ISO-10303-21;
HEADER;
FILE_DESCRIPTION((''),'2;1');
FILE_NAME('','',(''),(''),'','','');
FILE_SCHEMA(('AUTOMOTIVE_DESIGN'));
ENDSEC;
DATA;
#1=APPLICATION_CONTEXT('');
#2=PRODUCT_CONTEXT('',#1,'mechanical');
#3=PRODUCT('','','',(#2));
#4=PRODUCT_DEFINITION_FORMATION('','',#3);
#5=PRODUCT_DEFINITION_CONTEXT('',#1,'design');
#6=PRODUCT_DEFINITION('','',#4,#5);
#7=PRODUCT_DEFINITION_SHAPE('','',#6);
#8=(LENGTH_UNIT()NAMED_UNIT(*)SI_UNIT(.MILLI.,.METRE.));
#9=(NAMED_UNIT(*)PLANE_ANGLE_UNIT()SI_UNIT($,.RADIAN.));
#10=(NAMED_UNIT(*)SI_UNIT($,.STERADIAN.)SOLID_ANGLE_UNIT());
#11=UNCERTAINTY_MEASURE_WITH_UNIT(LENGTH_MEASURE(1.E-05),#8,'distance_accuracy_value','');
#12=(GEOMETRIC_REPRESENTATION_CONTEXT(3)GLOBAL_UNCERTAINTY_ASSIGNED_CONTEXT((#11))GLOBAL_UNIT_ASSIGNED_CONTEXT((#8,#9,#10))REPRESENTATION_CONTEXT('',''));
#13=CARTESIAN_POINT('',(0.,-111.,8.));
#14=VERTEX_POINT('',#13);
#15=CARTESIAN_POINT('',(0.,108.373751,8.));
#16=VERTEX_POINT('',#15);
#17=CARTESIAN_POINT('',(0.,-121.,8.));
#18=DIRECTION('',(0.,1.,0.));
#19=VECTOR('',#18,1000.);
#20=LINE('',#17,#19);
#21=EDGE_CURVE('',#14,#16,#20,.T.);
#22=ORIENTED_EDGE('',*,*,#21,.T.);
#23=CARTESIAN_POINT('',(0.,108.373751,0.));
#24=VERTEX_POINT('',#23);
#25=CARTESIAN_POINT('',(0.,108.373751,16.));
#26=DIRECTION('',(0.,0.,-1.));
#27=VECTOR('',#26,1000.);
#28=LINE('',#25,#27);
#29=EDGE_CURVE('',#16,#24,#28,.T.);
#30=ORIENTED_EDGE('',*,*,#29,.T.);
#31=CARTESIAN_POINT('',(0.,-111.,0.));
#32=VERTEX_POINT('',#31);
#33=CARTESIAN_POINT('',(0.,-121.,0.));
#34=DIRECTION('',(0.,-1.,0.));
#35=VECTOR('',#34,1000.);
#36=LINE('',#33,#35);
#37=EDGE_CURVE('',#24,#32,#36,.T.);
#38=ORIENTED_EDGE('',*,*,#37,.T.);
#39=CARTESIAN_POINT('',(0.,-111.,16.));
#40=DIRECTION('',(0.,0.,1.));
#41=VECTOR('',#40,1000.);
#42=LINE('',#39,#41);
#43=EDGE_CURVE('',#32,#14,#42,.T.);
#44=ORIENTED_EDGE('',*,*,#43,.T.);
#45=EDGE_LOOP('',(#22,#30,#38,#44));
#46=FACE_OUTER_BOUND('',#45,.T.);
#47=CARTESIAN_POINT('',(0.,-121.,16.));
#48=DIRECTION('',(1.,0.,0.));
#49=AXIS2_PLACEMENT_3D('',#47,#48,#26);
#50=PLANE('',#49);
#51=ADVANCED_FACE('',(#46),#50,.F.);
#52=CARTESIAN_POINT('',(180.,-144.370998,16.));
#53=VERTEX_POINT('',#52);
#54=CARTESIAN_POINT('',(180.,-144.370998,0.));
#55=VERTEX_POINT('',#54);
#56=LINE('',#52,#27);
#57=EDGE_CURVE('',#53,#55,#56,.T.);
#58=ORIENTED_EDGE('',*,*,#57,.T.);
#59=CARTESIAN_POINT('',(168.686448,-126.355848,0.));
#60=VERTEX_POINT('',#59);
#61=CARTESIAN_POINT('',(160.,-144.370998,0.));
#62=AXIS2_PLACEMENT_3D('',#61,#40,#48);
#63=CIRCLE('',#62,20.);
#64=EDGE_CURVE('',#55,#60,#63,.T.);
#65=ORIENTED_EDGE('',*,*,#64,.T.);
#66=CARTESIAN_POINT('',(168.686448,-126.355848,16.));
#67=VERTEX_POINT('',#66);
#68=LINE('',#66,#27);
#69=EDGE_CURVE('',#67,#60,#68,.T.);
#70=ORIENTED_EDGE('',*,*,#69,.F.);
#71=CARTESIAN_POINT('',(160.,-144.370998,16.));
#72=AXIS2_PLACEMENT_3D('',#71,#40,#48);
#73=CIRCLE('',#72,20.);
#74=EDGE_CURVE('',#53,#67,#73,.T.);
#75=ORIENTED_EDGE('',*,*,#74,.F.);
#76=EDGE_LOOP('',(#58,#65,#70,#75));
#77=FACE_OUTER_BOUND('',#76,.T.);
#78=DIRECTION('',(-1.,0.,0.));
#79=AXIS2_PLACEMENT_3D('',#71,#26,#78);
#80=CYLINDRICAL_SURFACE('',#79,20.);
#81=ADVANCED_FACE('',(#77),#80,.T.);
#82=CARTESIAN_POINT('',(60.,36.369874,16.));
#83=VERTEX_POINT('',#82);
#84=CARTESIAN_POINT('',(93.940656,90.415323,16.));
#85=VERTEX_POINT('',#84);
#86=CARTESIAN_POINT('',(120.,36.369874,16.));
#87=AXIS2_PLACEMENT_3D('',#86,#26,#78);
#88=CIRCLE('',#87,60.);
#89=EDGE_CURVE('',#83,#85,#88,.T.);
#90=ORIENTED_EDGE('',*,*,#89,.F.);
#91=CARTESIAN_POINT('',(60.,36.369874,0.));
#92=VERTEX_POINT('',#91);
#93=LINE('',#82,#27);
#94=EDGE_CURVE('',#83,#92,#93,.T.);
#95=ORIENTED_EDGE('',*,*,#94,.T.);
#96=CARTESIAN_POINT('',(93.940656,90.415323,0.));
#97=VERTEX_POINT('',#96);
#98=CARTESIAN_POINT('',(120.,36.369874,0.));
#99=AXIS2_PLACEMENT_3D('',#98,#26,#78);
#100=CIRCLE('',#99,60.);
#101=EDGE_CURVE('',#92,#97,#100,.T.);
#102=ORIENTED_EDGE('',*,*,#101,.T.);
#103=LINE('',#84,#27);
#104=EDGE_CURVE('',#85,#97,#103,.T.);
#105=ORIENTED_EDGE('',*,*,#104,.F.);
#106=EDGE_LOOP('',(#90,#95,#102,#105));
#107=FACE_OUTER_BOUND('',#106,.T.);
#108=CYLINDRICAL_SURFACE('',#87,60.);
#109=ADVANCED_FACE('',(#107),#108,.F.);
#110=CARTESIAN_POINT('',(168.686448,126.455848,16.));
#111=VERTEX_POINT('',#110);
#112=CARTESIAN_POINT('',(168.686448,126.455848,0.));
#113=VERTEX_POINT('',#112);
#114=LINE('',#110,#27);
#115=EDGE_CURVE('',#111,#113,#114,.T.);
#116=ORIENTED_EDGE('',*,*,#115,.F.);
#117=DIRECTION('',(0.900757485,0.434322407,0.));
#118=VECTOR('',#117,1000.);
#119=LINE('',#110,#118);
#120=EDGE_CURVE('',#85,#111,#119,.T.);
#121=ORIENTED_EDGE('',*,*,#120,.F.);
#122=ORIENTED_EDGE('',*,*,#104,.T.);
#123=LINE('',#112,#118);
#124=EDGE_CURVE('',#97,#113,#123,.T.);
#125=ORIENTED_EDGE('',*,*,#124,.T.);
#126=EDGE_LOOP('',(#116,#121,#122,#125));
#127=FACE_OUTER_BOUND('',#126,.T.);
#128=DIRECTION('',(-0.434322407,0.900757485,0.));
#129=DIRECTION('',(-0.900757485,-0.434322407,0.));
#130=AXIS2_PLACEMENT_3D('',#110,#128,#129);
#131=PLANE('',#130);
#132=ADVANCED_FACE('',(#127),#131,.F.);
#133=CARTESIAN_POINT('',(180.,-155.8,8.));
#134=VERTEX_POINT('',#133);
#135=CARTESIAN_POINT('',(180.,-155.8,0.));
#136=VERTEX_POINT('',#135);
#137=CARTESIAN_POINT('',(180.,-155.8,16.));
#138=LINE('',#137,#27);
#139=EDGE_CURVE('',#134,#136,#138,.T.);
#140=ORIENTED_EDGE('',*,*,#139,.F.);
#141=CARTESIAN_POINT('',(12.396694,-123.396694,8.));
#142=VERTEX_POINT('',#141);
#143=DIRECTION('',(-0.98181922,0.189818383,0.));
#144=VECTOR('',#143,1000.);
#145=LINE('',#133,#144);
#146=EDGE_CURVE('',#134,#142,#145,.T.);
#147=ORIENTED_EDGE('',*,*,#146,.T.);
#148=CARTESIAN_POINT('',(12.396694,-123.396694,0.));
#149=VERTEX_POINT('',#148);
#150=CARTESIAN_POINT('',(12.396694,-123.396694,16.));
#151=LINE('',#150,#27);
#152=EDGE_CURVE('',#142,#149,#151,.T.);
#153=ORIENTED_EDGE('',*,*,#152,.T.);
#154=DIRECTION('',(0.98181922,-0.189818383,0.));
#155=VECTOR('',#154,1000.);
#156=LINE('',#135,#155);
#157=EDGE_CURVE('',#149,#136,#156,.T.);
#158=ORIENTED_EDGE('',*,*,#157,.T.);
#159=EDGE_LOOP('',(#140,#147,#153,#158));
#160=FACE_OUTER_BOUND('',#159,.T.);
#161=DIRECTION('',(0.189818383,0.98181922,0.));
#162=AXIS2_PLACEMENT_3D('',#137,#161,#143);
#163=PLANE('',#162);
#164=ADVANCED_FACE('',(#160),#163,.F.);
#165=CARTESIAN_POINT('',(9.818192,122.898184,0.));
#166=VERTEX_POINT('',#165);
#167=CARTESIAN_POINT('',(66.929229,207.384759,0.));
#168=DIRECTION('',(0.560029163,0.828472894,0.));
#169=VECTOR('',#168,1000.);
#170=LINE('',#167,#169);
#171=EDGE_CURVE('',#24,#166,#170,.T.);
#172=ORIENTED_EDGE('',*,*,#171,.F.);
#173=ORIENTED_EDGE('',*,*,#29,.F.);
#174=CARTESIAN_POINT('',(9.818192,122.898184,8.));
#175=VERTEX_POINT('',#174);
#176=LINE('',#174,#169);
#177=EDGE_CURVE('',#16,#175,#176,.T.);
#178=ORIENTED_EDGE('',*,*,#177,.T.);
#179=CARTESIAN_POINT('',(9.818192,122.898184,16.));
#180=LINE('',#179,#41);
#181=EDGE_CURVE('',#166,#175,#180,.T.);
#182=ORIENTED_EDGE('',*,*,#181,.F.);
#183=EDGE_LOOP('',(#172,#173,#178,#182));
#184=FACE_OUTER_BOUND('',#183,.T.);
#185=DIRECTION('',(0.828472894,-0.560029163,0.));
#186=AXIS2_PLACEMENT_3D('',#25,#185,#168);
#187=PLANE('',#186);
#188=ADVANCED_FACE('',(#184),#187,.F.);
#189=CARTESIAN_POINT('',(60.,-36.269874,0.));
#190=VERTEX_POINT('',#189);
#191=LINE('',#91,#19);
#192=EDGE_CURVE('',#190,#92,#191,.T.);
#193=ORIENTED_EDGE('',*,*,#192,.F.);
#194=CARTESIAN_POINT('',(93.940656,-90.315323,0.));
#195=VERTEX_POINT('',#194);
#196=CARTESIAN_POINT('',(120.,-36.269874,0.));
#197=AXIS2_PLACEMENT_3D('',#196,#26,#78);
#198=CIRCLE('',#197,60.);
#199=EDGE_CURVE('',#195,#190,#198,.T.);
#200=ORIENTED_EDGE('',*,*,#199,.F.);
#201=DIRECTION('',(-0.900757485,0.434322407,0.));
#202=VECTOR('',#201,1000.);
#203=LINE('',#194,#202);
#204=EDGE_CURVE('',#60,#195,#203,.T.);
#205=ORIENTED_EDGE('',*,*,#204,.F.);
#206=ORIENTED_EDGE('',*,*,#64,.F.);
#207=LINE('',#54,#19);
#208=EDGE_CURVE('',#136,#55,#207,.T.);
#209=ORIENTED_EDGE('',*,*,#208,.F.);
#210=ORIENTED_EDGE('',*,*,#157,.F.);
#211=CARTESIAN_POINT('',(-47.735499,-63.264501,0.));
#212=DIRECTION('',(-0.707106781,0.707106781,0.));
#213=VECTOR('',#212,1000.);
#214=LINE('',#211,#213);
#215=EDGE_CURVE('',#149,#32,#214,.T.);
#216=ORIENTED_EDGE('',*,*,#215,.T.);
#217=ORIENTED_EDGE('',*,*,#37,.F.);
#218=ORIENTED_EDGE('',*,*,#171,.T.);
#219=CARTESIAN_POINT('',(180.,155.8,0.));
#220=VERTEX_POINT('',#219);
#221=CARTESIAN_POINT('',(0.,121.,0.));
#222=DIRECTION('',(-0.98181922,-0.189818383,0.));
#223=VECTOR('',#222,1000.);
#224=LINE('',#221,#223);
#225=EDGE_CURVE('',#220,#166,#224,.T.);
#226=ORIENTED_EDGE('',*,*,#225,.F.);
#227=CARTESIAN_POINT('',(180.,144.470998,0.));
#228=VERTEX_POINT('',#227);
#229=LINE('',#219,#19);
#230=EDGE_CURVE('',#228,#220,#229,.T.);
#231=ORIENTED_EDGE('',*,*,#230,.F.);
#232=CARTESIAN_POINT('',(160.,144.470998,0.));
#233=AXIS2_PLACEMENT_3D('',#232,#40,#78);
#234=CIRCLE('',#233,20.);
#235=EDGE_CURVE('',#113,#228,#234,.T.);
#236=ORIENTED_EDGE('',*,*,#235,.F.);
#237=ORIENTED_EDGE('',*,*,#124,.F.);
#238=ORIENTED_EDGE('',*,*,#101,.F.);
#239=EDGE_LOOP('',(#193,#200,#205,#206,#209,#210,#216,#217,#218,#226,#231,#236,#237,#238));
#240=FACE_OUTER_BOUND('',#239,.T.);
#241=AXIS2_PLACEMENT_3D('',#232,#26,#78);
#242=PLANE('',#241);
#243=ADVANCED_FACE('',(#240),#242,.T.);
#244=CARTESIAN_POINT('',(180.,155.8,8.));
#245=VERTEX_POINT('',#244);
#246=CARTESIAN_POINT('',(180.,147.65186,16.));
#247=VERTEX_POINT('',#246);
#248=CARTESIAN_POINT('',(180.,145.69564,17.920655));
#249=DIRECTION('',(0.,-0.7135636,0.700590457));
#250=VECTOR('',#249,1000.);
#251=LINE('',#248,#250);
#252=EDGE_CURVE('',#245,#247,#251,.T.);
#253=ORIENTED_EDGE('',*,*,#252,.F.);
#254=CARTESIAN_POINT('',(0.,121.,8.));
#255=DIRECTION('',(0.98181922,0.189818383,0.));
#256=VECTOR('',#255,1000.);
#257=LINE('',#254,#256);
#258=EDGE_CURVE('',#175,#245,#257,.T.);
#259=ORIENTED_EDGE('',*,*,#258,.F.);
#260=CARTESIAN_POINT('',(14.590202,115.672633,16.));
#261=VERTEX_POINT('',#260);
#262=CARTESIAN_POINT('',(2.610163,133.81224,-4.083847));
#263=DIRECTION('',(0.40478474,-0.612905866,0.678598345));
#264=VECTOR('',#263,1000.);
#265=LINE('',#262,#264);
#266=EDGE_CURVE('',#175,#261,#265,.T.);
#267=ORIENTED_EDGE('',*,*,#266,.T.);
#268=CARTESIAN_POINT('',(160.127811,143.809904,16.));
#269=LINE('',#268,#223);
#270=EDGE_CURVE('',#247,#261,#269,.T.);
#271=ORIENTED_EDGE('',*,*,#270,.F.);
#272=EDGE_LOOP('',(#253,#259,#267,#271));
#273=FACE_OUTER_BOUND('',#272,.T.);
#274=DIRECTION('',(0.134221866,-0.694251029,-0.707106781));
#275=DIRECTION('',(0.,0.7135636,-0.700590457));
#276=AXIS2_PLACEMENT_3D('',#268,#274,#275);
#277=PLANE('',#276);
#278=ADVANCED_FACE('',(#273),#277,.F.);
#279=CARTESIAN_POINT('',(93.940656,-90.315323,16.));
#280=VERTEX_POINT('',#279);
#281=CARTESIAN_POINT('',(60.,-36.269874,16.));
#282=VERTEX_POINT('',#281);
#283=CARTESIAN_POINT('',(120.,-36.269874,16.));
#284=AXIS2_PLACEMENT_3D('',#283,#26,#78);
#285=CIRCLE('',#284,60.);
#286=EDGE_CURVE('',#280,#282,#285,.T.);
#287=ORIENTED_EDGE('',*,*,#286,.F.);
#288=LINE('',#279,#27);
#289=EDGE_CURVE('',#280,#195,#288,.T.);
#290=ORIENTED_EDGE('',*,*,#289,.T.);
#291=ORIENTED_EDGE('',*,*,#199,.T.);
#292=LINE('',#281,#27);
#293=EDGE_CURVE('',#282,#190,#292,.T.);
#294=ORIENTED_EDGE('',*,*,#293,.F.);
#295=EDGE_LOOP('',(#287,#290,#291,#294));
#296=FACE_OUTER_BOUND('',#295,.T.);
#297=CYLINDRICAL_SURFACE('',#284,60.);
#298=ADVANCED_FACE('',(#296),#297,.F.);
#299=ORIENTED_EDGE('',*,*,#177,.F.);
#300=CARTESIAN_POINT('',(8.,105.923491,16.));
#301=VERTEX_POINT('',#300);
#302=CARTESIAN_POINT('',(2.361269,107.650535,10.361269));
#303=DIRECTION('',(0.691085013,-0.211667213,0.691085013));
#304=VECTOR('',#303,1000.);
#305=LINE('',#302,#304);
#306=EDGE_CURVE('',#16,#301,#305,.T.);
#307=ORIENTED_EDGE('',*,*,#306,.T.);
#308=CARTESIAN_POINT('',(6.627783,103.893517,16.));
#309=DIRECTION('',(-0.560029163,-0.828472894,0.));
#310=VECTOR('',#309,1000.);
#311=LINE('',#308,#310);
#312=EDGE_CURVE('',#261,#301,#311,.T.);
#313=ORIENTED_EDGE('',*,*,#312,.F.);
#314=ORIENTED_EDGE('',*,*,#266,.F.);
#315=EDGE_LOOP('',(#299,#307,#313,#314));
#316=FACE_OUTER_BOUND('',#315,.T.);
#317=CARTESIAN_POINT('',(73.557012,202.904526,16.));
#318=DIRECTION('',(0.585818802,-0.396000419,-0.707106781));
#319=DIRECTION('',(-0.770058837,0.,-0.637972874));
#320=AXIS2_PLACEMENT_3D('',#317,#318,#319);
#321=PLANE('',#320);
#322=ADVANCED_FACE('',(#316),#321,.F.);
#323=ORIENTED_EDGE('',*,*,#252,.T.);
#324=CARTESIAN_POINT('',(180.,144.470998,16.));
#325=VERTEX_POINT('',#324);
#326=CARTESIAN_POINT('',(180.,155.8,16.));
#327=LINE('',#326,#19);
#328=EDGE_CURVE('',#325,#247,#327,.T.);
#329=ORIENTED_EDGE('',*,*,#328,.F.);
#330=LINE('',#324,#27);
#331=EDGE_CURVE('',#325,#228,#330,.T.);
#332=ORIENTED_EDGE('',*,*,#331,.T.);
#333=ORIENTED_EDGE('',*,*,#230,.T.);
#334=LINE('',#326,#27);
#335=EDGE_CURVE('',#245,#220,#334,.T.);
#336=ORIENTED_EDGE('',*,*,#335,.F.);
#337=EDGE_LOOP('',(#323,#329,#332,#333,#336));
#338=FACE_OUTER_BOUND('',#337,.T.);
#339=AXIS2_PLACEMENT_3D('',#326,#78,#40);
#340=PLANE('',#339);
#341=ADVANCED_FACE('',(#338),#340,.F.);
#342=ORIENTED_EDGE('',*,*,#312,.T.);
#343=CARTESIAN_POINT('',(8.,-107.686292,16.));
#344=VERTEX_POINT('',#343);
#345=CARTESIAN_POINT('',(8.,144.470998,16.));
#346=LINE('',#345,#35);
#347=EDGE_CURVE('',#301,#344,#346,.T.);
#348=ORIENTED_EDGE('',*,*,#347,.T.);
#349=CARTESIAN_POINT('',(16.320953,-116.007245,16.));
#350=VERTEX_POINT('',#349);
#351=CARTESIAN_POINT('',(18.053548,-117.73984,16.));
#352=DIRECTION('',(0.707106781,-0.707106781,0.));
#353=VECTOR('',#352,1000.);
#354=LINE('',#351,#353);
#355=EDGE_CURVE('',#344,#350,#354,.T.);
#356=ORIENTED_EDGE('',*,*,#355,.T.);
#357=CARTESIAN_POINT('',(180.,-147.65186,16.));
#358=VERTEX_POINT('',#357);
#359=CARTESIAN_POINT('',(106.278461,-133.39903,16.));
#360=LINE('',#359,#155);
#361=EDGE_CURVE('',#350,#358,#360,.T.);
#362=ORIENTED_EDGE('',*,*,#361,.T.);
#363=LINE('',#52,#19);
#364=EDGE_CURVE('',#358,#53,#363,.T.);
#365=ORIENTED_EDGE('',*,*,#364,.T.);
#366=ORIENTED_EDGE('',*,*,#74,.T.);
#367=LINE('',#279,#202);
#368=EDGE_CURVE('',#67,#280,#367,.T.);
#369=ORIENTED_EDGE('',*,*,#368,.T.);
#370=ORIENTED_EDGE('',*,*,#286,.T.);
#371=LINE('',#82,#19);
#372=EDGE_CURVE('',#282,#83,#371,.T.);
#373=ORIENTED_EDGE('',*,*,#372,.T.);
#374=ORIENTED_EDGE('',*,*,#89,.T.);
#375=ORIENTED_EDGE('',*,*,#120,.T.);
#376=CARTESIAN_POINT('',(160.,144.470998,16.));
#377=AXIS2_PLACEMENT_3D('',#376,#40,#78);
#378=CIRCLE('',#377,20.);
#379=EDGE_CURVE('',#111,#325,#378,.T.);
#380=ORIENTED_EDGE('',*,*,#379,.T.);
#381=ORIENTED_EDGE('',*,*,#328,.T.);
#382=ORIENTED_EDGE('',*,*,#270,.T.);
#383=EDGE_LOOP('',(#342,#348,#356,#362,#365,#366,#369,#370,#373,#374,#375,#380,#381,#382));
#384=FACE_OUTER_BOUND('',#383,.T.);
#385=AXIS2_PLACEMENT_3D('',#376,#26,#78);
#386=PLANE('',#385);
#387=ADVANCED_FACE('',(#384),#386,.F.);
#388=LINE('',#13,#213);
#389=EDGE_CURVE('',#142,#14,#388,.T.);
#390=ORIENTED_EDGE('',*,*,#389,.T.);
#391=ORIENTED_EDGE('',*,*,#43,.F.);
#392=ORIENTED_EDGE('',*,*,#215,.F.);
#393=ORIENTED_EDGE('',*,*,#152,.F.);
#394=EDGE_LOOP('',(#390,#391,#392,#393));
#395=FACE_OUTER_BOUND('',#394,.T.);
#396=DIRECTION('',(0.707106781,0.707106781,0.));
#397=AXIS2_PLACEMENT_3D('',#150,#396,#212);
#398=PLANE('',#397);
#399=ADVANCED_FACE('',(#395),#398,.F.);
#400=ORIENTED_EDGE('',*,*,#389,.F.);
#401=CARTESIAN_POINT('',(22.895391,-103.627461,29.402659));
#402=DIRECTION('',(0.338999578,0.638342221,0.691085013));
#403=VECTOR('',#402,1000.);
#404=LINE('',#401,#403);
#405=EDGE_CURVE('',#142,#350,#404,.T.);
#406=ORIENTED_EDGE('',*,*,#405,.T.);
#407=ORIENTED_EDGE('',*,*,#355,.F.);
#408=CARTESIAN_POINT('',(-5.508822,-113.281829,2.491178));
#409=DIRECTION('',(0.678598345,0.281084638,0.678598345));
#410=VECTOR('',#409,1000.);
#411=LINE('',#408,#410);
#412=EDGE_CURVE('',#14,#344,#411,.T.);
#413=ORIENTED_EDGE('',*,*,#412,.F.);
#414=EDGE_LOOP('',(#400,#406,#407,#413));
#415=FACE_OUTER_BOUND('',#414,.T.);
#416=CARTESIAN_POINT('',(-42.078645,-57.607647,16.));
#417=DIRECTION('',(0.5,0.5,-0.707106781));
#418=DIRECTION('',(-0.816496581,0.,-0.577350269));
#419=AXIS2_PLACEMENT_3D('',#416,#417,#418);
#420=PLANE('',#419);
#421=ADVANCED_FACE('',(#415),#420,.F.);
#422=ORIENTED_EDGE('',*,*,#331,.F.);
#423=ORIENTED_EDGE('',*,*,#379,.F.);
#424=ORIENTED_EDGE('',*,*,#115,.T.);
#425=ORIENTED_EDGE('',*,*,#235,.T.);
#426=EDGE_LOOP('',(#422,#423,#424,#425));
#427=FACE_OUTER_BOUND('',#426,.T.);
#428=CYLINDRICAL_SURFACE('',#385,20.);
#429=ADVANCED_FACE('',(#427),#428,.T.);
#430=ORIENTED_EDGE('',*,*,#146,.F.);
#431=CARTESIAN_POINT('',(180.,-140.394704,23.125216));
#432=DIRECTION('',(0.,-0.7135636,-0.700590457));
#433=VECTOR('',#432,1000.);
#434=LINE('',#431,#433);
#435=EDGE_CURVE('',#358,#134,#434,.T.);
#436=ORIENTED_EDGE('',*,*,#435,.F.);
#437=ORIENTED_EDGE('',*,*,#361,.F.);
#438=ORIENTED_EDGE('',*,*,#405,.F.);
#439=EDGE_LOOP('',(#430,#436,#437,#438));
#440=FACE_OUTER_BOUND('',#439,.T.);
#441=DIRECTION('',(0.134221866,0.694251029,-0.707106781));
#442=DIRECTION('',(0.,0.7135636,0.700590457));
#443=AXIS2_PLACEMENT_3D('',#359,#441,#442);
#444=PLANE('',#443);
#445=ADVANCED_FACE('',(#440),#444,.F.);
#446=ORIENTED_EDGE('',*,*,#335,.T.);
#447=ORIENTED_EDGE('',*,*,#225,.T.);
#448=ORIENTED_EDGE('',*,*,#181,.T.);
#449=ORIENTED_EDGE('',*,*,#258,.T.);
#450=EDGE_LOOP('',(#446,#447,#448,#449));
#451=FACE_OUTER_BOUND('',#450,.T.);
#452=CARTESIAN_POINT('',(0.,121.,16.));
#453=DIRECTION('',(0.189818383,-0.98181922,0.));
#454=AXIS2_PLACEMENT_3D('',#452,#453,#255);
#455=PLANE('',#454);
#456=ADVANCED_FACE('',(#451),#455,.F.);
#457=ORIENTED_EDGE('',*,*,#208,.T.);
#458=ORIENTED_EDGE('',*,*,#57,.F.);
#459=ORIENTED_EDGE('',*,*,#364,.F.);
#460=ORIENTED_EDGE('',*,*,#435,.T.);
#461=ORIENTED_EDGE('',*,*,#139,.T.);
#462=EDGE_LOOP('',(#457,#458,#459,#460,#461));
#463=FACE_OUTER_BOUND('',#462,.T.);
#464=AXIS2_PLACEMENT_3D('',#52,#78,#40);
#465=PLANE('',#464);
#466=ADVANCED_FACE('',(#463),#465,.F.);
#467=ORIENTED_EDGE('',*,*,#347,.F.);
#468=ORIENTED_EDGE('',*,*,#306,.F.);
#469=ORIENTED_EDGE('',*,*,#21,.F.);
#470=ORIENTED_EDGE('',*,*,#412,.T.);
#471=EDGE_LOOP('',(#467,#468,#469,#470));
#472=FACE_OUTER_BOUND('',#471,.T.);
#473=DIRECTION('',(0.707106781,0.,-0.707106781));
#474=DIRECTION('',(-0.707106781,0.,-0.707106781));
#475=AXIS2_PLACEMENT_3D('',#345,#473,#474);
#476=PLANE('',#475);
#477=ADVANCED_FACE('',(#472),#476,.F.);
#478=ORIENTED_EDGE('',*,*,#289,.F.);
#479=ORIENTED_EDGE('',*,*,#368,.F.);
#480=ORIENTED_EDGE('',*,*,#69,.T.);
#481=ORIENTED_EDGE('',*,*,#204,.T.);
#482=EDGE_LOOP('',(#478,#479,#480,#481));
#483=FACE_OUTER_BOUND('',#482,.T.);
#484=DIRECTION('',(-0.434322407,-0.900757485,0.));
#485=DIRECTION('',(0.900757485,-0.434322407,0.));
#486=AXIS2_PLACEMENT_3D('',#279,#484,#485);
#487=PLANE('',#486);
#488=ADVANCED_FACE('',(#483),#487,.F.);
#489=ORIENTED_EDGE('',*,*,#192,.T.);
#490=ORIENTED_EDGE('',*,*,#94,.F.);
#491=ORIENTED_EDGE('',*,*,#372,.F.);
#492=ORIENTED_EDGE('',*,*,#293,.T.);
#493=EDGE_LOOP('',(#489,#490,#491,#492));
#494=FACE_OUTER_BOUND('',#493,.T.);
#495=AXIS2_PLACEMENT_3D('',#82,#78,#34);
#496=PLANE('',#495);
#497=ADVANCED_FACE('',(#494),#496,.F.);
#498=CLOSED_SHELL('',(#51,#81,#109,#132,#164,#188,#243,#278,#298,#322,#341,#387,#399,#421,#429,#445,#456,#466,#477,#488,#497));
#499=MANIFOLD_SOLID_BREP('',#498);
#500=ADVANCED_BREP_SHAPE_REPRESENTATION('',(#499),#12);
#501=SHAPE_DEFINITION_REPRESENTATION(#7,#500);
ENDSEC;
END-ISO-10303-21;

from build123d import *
from OCP.BRepFilletAPI import BRepFilletAPI_MakeChamfer

# Parameters (mm, degrees)
BOSS_EXTRUDE1_DEPTH = 16
CHAMFER1_SIZE       = 10
CHAMFER1_SIZE2      = 12.62624927
CHAMFER2_SIZE       = 8


with BuildPart() as part:
    # Sketch1 → Boss-Extrude1 (new body)
    with BuildSketch(Plane.XY):
        with BuildLine():
            Line((0, -121), (0, 121))
            Line((0, 121), (180, 155.8))
            Line((180, 155.8), (180, 144.470997586))
            ThreePointArc((180, 144.470997586), (176.937074168, 133.834479423), (168.686448136, 126.455847884))
            Line((168.686448136, 126.455847884), (93.940655591, 90.415323041))
            ThreePointArc((93.940655591, 90.415323041), (69.188777497, 68.279428426), (60, 36.369873936))
            Line((60, 36.369873936), (60, -36.269873936))
            ThreePointArc((60, -36.269873936), (69.188777497, -68.179428426), (93.940655591, -90.315323041))
            Line((93.940655591, -90.315323041), (168.686448136, -126.355847884))
            ThreePointArc((168.686448136, -126.355847884), (176.937074168, -133.734479423), (180, -144.370997586))
            Line((180, -144.370997586), (180, -155.8))
            Line((180, -155.8), (0, -121))
        make_face()
    extrude(amount=BOSS_EXTRUDE1_DEPTH)

    # Chamfer1: one chamfer whose edges measure the first distance from different faces: ONE call of the kernel's chamfer builder (chamfer() names one face for all edges)
    chamfer1_edges_1 = [part.edges().sort_by_distance(p)[0] for p in [
        (0, -121, 8),
    ]]
    chamfer1_side_1 = [part.faces().sort_by_distance(p)[0] for p in [
        (0, 0, 8),
    ]]
    chamfer1_edges_2 = [part.edges().sort_by_distance(p)[0] for p in [
        (0, 121, 8),
    ]]
    chamfer1_side_2 = [part.faces().sort_by_distance(p)[0] for p in [
        (90, 138.4, 8),
    ]]
    chamfer1 = BRepFilletAPI_MakeChamfer(part.part.solid().wrapped)
    for e in chamfer1_edges_1:
        chamfer1.Add(CHAMFER1_SIZE, CHAMFER1_SIZE2, e.wrapped, chamfer1_side_1[0].wrapped)  # the first distance lies on this face
    for e in chamfer1_edges_2:
        chamfer1.Add(CHAMFER1_SIZE, CHAMFER1_SIZE2, e.wrapped, chamfer1_side_2[0].wrapped)  # the first distance lies on this face
    add(Compound.cast(chamfer1.Shape()), mode=Mode.REPLACE)

    # Chamfer2
    chamfer2_edges = [part.edges().sort_by_distance(p)[0] for p in [
        (0, -1.313124635, 16),
        (96.198347107, -139.598347107, 16),
        (6.198347107, -117.198347107, 16),
        (4.909096102, 115.635967278, 16),
        (94.909096102, 139.349091913, 16),
    ]]
    chamfer(chamfer2_edges, length=CHAMFER2_SIZE)


solid = part.part
